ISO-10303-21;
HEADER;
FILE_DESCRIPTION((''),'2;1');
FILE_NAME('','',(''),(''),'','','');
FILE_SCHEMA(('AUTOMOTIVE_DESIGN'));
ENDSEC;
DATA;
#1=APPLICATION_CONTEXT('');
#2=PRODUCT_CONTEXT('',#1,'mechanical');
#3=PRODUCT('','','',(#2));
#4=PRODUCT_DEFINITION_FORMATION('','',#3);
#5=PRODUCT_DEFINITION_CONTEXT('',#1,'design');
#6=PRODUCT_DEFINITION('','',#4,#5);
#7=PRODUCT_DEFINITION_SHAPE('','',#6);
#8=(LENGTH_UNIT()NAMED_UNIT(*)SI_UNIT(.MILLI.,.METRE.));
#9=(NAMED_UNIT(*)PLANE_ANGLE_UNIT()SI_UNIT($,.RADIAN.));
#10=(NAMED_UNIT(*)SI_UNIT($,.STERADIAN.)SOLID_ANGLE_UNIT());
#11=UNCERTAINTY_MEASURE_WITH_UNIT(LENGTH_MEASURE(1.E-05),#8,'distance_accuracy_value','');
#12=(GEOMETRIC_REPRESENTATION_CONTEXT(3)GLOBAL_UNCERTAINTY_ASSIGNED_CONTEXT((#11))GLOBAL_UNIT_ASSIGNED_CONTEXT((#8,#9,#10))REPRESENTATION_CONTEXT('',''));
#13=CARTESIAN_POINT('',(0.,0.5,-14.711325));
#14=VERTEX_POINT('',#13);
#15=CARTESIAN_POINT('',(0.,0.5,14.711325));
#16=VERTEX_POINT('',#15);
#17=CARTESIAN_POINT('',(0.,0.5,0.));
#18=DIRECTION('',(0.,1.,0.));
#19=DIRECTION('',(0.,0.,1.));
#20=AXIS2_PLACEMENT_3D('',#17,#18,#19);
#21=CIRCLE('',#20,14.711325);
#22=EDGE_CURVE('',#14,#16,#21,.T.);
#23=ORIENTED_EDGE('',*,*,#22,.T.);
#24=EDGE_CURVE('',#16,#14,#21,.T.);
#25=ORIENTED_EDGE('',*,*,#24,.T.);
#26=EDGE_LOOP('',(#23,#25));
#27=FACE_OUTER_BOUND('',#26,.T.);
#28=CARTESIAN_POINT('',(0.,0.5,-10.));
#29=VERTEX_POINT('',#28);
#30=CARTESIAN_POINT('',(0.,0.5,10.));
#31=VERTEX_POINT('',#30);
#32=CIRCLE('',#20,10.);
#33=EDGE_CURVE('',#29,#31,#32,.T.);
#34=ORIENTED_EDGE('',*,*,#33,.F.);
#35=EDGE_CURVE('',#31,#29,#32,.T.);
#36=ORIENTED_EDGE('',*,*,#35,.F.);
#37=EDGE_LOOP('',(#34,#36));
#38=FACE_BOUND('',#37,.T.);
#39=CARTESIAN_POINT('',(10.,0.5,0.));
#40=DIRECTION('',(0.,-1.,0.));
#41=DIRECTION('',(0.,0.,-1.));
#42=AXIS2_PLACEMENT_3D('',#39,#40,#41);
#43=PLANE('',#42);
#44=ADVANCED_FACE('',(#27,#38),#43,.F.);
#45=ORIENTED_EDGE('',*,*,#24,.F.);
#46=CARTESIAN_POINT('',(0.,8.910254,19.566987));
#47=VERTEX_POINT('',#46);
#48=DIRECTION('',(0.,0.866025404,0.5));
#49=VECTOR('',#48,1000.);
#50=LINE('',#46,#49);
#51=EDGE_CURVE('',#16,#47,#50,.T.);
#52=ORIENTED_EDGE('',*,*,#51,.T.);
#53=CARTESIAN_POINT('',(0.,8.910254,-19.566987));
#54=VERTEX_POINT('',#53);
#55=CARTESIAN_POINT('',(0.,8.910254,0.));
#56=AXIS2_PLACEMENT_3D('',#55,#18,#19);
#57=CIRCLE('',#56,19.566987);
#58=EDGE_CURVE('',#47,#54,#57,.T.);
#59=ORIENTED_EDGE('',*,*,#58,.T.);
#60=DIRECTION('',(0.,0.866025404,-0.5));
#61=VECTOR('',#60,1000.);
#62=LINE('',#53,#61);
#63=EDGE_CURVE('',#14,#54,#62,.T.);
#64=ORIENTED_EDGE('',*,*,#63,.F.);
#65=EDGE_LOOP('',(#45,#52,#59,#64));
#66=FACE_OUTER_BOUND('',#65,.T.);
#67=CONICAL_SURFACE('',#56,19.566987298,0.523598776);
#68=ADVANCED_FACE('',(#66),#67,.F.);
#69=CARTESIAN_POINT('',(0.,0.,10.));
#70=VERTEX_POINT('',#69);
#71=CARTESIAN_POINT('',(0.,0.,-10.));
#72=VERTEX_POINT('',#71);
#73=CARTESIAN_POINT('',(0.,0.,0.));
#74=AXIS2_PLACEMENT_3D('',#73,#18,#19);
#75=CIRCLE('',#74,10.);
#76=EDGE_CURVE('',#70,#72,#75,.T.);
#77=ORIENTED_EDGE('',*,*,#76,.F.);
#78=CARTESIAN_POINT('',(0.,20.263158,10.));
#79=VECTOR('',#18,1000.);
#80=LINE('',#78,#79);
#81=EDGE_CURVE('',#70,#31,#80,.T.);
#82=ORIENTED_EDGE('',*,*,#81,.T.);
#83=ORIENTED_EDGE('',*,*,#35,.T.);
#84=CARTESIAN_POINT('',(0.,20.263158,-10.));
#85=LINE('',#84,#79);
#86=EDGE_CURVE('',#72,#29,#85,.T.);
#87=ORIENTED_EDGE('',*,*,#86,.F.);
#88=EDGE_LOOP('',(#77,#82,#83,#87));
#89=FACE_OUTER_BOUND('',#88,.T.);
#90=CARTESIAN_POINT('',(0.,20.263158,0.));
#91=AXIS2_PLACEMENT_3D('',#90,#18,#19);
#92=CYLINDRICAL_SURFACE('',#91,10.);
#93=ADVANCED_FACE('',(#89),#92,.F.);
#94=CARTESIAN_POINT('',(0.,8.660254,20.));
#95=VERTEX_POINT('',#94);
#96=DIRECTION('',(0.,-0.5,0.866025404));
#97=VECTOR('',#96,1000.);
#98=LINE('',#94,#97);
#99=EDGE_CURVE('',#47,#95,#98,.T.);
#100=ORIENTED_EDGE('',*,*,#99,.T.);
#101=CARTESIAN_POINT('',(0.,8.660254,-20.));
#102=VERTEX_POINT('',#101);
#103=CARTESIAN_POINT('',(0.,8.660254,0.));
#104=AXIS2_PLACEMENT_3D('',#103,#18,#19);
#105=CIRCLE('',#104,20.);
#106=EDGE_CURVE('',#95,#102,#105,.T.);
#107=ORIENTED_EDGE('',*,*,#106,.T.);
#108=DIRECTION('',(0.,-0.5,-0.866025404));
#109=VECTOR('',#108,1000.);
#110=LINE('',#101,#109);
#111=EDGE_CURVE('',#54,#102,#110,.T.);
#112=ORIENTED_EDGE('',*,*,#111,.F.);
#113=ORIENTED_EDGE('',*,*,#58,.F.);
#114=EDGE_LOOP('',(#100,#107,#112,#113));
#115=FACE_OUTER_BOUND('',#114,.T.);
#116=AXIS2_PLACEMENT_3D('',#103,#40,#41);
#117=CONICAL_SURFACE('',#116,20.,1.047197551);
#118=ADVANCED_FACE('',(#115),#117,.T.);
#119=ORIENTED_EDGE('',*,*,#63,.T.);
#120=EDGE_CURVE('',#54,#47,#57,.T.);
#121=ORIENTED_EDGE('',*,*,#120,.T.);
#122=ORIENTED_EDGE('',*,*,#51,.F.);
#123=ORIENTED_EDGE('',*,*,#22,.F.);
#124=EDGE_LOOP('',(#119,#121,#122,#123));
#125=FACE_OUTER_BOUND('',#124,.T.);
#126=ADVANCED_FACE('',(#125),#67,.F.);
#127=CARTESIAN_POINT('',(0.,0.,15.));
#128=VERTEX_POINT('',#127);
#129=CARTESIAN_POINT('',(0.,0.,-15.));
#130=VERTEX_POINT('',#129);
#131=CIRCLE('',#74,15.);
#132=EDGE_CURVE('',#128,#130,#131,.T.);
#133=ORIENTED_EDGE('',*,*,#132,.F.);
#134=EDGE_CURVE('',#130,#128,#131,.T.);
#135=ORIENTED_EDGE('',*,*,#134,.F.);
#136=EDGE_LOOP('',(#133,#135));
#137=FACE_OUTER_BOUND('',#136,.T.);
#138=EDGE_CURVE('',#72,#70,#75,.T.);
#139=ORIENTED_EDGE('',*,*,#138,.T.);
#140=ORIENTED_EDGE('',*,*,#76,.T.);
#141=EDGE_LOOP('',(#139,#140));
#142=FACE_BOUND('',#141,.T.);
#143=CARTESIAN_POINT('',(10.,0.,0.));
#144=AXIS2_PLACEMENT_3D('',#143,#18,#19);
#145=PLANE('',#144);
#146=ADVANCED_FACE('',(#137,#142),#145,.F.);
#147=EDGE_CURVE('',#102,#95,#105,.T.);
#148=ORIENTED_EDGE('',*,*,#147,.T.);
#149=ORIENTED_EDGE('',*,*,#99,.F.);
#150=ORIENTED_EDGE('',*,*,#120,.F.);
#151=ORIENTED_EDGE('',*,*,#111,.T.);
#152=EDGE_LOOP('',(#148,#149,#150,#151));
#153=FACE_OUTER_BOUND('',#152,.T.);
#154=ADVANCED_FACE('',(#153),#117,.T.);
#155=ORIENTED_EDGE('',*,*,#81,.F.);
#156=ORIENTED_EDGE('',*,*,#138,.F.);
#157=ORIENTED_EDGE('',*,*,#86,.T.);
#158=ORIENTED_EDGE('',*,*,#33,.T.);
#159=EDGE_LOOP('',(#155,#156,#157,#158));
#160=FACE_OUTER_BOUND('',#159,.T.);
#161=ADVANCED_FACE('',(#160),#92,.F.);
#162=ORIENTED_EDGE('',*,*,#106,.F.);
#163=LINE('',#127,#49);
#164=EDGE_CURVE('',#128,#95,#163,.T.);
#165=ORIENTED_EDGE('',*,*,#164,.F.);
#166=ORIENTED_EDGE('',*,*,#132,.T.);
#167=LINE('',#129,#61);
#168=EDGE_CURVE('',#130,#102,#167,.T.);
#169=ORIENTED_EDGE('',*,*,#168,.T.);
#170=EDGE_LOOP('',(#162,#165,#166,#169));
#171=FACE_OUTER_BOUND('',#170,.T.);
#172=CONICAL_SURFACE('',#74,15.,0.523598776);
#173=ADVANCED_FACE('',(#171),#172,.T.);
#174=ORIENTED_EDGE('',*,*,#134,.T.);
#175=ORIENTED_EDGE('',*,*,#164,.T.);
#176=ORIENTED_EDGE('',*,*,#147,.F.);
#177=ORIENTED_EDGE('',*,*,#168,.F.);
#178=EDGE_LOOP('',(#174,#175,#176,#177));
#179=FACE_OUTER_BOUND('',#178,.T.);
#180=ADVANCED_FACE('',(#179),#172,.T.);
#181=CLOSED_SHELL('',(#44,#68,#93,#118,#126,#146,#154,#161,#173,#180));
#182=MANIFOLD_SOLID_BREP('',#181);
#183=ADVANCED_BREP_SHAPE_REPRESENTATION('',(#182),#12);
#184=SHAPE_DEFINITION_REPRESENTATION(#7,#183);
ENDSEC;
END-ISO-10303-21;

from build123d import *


with BuildPart() as part:
    # Sketch1 → Revolve1 (revolve)
    with BuildSketch(Plane.XY, mode=Mode.PRIVATE) as revolve1_sk:
        Polygon((10, 0), (15, 0), (20, 8.660254038), (19.566987298, 8.910254038), (14.711324865, 0.5), (10, 0.5), align=None)
    revolve(revolve1_sk.sketch.rotate(Axis((0, 20.263157895, 0), (0, -1, 0)), 90), axis=Axis((0, 20.263157895, 0), (0, -1, 0)))


solid = part.part
